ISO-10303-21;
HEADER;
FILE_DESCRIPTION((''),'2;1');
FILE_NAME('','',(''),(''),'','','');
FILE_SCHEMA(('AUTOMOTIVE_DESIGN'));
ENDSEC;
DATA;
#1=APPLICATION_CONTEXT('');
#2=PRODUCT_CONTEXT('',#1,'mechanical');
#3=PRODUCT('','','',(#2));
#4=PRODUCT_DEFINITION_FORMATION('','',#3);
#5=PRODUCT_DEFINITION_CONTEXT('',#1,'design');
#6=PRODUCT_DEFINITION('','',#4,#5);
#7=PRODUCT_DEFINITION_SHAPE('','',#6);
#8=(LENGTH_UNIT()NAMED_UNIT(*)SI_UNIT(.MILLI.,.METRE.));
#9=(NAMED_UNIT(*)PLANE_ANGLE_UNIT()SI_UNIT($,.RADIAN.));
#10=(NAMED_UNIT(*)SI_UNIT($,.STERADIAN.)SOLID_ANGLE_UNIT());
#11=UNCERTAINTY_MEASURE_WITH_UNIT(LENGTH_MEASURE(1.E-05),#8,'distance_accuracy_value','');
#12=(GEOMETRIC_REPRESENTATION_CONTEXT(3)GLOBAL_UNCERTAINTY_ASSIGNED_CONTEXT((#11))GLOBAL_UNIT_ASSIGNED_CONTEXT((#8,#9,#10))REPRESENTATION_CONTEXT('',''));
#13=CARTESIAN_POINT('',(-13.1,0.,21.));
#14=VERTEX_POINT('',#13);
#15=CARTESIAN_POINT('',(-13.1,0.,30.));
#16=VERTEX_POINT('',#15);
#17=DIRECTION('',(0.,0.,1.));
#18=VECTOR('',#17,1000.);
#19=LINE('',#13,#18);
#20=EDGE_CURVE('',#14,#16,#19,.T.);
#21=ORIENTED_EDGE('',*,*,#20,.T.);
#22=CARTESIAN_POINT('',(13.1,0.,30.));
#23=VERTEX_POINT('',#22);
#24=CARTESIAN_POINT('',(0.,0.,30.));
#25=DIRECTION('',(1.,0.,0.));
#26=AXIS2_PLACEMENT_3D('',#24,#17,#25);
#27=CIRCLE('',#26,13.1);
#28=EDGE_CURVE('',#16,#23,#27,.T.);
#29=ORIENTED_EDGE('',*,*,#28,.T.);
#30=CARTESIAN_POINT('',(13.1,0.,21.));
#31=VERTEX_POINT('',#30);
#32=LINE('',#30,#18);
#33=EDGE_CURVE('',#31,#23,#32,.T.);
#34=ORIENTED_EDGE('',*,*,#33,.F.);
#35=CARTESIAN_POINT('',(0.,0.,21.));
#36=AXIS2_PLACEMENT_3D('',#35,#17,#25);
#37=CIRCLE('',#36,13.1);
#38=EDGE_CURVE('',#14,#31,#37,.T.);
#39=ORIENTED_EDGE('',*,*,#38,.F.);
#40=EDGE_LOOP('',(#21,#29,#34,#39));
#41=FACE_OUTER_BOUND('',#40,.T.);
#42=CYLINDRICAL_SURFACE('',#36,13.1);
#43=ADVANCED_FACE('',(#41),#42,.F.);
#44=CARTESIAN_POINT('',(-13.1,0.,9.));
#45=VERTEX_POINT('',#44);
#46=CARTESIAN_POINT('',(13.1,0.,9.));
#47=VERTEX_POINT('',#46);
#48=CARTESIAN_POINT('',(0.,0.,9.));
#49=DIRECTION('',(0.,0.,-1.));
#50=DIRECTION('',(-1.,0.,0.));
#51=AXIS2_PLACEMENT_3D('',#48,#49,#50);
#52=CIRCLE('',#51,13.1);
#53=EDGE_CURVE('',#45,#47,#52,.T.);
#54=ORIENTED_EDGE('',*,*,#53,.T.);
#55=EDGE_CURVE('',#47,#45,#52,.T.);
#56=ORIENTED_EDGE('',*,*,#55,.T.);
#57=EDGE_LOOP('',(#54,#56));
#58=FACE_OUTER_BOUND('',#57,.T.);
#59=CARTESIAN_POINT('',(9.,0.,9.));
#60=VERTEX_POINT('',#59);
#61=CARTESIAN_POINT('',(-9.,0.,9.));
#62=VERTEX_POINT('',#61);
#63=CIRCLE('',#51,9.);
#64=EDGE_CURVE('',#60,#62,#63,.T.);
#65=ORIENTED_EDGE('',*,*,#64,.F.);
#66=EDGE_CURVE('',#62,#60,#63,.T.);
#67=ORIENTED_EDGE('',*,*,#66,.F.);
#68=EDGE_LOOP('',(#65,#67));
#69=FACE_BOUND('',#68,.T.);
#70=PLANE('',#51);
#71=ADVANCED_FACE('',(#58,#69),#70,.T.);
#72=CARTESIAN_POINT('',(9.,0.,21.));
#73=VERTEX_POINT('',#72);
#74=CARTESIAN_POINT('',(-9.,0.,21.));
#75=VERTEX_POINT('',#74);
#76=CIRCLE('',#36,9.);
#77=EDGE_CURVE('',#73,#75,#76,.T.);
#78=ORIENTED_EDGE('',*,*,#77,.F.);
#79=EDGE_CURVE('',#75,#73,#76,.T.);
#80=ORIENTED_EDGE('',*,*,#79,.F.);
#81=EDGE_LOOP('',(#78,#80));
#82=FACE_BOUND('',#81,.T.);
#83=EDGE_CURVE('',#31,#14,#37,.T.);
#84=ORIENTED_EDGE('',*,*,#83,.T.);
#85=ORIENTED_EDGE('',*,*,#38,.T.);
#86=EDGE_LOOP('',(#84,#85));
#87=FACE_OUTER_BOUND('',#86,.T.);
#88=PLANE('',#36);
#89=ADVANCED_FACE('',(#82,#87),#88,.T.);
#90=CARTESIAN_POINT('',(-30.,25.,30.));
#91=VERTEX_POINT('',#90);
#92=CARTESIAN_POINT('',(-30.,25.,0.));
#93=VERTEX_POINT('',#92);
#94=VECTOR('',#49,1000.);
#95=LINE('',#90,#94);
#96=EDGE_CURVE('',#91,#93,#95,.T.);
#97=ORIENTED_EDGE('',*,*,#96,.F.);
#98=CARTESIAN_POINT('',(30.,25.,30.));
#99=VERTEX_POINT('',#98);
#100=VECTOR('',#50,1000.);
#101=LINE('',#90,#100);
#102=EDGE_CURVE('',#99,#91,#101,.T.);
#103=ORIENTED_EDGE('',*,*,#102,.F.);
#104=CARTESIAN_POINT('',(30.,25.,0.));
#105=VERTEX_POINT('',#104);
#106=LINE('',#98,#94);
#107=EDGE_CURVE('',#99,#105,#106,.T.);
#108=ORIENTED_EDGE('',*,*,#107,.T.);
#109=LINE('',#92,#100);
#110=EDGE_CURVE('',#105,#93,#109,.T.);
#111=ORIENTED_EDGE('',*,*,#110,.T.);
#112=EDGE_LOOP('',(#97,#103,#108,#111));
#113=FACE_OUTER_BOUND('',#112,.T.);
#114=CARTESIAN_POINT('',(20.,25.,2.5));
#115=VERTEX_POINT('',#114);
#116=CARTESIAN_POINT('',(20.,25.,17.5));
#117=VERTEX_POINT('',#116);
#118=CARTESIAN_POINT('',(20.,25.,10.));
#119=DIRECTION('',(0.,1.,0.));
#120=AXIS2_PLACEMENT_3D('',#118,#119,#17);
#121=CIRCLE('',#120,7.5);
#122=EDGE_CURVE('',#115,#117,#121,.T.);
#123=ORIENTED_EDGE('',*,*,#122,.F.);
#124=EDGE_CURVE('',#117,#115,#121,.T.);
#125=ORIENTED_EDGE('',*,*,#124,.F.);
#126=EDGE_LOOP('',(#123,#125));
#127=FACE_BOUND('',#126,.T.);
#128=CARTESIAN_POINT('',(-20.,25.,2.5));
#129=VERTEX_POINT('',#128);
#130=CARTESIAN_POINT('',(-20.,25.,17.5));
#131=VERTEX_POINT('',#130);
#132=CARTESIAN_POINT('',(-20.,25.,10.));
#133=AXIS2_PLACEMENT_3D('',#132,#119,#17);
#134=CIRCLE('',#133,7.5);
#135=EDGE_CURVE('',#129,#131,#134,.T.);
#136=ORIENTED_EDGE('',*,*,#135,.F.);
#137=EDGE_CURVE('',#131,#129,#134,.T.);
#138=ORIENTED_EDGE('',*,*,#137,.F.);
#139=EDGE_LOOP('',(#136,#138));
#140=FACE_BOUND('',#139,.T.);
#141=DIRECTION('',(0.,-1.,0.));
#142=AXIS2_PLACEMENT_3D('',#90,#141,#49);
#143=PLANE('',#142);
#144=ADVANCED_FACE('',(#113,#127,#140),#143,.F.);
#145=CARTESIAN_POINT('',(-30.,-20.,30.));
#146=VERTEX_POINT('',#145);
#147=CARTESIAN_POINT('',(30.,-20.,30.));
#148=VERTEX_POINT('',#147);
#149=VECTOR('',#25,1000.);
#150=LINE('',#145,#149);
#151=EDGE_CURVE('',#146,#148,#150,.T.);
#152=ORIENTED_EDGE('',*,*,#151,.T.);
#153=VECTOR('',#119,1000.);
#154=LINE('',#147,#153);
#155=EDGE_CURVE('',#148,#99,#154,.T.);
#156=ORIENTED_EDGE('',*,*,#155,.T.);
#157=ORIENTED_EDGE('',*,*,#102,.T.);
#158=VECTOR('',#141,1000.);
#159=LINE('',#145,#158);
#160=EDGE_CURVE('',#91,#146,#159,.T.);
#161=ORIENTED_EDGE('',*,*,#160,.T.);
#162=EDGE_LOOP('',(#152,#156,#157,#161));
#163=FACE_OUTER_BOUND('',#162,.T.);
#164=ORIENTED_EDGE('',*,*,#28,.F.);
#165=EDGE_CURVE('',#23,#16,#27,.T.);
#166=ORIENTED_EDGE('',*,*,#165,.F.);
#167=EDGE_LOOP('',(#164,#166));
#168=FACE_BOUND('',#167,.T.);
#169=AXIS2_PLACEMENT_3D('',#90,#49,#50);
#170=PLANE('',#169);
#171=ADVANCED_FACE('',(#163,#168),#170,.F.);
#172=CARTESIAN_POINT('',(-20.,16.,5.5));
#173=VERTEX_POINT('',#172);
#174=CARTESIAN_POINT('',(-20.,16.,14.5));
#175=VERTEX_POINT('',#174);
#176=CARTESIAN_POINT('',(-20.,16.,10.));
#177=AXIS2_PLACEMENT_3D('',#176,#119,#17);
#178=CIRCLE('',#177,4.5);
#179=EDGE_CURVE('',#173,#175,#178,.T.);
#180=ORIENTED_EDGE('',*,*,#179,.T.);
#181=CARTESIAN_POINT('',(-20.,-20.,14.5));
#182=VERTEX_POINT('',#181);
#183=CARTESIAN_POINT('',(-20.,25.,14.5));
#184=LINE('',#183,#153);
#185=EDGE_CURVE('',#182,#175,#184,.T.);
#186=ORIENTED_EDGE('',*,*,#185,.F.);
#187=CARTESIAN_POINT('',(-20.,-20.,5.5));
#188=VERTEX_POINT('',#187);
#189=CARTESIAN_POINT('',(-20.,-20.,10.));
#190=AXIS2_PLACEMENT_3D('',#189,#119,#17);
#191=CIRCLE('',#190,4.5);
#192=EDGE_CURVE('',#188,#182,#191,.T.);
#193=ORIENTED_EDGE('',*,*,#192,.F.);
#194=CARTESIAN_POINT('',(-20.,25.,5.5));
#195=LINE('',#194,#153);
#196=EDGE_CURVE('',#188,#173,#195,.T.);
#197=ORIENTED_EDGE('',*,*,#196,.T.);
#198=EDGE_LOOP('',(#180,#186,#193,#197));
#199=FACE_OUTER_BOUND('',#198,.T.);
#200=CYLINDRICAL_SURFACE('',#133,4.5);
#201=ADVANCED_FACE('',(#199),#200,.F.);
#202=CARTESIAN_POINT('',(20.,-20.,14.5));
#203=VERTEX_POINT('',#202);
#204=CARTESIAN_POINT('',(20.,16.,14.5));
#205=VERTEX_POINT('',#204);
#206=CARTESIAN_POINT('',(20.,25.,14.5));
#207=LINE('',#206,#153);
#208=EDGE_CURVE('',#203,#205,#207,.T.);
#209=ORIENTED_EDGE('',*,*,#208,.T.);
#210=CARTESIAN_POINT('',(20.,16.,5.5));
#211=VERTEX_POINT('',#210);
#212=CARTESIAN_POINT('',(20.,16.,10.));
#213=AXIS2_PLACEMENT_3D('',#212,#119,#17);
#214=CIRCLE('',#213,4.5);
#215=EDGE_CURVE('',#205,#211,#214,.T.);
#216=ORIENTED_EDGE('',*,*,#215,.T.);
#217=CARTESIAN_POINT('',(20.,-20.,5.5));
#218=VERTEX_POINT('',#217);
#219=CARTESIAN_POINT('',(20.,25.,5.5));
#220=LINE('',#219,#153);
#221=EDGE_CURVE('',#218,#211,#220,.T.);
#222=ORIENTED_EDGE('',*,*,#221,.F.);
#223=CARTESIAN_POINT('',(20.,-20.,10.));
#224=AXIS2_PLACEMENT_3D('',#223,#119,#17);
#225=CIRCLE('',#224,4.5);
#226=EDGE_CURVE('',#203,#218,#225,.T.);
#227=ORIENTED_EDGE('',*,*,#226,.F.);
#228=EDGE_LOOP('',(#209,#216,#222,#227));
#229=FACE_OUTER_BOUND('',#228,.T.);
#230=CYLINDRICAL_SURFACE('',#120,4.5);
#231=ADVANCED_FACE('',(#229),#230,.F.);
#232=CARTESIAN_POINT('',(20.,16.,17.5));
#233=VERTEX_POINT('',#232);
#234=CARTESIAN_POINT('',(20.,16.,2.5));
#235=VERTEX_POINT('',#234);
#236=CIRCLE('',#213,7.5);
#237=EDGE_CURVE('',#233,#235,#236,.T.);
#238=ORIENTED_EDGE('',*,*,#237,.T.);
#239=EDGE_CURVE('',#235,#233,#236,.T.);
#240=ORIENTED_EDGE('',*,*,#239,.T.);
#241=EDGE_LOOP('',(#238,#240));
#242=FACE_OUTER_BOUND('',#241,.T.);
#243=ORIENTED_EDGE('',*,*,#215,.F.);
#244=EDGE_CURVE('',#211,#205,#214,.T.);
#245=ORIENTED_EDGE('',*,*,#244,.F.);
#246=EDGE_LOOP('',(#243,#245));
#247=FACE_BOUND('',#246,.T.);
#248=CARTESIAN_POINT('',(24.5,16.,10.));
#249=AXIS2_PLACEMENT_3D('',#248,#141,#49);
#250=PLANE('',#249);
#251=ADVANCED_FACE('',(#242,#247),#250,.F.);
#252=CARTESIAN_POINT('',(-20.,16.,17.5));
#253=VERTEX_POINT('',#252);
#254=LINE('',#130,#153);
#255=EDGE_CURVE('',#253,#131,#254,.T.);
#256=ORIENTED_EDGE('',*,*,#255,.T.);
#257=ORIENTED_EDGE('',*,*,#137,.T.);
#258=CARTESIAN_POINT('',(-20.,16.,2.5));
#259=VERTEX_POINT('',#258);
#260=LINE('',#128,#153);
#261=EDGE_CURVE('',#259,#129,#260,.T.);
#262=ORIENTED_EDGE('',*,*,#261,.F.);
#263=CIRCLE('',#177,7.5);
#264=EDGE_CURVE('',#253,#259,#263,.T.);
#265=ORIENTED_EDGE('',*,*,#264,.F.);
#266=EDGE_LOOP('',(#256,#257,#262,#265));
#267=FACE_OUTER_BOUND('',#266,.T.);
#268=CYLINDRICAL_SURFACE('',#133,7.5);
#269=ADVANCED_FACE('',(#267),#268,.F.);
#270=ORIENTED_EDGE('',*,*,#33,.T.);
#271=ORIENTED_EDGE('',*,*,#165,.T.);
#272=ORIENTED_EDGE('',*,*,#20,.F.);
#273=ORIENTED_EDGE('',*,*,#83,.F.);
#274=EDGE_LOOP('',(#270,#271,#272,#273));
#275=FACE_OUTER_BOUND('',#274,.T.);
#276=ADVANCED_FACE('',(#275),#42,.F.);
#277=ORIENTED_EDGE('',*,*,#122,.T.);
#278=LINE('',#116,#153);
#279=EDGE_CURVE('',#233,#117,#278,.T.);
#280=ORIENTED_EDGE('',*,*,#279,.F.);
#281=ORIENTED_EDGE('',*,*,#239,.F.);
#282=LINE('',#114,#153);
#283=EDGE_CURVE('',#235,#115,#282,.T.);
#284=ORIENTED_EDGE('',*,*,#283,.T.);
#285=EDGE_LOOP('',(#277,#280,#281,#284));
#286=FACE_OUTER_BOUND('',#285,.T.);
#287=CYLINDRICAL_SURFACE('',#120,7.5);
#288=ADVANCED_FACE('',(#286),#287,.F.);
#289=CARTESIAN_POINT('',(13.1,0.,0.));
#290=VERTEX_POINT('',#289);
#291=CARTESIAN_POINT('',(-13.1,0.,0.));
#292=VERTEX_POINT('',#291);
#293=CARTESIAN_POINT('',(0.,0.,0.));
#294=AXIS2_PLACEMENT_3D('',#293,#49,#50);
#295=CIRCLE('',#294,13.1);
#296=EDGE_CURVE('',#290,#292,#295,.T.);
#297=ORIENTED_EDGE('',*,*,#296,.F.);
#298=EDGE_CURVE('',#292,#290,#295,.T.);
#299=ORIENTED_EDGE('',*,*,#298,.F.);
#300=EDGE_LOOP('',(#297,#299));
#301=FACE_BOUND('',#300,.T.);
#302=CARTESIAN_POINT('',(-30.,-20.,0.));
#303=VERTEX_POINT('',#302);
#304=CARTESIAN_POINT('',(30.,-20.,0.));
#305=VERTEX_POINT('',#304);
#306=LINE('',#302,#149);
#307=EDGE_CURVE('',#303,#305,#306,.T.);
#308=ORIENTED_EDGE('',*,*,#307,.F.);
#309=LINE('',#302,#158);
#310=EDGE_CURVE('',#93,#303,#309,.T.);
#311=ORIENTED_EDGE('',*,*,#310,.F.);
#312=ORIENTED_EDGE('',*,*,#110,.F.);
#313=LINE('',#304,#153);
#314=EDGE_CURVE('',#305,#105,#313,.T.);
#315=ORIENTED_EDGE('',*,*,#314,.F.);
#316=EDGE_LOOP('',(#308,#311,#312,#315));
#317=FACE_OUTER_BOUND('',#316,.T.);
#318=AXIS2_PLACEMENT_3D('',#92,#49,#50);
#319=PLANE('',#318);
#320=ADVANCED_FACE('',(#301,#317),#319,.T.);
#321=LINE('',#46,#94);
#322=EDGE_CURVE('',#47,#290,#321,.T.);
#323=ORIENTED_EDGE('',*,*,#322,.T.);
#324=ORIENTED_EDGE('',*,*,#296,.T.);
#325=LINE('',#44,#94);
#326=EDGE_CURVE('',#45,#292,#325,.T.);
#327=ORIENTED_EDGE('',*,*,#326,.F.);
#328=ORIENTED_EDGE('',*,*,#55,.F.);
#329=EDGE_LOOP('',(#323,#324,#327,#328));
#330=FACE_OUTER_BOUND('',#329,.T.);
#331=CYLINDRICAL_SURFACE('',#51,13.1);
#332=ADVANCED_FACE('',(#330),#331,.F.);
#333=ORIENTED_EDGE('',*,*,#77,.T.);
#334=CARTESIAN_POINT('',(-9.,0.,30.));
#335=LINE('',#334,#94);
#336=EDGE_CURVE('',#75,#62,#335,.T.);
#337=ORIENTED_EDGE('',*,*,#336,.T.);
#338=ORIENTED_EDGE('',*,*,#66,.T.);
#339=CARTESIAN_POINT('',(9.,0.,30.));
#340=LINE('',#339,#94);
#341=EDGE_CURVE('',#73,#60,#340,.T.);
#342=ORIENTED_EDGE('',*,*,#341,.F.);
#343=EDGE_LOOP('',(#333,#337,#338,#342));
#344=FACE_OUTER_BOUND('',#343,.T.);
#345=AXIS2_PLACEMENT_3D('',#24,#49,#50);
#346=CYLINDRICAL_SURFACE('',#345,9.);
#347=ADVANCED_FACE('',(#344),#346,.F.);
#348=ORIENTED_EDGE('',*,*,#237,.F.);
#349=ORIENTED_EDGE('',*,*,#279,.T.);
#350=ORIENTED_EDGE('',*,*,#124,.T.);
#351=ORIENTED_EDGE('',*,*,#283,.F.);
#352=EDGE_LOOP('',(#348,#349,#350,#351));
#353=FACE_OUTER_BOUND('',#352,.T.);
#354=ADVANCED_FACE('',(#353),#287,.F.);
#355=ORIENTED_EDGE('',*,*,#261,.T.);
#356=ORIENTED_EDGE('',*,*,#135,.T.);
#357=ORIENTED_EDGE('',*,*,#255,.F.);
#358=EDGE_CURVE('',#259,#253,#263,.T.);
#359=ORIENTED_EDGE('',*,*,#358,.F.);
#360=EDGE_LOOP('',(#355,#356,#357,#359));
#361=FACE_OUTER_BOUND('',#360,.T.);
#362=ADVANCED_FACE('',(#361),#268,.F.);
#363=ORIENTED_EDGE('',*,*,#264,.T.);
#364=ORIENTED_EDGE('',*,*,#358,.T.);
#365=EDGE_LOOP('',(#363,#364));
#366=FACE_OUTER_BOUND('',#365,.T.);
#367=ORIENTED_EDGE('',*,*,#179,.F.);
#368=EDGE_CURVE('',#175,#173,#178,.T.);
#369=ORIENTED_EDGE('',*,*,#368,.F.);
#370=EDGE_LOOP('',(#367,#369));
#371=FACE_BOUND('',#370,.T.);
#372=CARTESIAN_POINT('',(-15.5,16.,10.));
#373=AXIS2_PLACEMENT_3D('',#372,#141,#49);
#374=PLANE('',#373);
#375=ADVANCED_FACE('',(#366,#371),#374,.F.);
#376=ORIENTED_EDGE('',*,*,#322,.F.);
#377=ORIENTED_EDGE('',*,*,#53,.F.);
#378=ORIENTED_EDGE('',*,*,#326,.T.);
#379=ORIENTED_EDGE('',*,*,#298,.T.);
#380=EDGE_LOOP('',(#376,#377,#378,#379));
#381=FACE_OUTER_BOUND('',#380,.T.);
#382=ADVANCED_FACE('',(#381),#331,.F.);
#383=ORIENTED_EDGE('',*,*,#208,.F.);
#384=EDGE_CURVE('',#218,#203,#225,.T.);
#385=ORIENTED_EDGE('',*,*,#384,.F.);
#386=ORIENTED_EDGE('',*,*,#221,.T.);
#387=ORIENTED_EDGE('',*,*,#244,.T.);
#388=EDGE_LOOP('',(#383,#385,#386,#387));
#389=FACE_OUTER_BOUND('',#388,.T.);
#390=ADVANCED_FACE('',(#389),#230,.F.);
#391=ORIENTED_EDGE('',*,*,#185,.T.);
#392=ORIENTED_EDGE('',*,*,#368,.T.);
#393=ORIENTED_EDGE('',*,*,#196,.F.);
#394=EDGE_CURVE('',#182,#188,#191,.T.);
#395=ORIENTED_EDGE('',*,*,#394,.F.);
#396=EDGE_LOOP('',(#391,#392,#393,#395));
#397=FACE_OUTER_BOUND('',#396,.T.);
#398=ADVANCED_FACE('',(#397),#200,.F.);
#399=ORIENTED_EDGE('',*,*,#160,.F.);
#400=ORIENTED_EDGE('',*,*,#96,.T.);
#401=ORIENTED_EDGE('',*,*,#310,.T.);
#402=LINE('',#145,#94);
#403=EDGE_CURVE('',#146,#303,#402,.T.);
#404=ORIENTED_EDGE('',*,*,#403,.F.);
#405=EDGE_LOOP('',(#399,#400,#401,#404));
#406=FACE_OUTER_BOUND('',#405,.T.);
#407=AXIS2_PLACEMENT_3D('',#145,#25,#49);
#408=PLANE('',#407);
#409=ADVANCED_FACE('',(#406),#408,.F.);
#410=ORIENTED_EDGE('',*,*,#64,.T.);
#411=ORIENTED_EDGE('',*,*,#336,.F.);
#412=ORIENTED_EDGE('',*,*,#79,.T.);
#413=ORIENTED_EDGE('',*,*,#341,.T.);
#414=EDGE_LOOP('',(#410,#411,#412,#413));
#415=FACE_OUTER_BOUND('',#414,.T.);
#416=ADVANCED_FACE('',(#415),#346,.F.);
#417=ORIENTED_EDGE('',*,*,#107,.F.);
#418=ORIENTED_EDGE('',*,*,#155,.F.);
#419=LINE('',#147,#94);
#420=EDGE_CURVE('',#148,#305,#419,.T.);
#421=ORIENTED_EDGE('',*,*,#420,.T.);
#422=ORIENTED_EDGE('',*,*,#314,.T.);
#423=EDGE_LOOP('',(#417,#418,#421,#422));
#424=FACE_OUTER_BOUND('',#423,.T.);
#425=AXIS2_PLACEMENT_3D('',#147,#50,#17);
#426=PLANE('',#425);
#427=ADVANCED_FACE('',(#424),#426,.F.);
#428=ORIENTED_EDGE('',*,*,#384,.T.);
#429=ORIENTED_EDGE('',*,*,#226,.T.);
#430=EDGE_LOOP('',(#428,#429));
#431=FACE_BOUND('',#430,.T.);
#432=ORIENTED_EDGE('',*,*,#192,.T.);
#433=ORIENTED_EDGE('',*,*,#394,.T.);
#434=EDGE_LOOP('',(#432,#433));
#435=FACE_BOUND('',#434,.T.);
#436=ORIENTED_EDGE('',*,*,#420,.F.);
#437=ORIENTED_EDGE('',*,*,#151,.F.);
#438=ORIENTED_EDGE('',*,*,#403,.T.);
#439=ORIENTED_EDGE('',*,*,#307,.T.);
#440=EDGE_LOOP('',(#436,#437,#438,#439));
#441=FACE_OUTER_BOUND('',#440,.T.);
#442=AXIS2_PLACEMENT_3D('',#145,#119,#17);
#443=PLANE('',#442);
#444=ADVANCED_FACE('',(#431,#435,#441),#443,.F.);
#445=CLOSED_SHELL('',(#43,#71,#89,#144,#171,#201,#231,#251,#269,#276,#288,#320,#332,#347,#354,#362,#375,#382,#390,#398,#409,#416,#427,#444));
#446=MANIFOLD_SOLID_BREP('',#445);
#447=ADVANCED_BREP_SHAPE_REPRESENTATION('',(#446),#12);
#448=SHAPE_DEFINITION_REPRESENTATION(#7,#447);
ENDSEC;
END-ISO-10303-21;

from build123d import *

# Parameters (mm, degrees)
SKETCH1_W                                            = 60
SKETCH1_H                                            = 45
SKETCH1_R                                            = 9
BOSS_EXTRUDE1_DEPTH                                  = 30
HOLE_SIZE_PER_SOCKET_HEAD_CAP_SCREW_TYPE_D           = 9
HOLE_SIZE_PER_SOCKET_HEAD_CAP_SCREW_TYPE_CBORE_D     = 15
HOLE_SIZE_PER_SOCKET_HEAD_CAP_SCREW_TYPE_CBORE_DEPTH = 9
SKETCH2_R                                            = 13.1
EXTRUDE1_DEPTH                                       = 9
EXTRUDE2_START                                       = -9
SKETCH3_R                                            = 13.1
EXTRUDE2_DEPTH                                       = 9


with BuildPart() as part:
    # Sketch1 → Boss-Extrude1 (new body)
    with BuildSketch(Plane.XY):
        with Locations((0, 2.5)):
            Rectangle(SKETCH1_W, SKETCH1_H)
        Circle(SKETCH1_R, mode=Mode.SUBTRACT)
    extrude(amount=BOSS_EXTRUDE1_DEPTH)

    # Hole size per socket head cap screw type1 (through all)
    with Locations(Plane(origin=(0, 25, 0), x_dir=(-1, 0, 0), z_dir=(0, 1, 0))):
        with Locations((20, 10), (-20, 10)):
            CounterBoreHole(HOLE_SIZE_PER_SOCKET_HEAD_CAP_SCREW_TYPE_D / 2, HOLE_SIZE_PER_SOCKET_HEAD_CAP_SCREW_TYPE_CBORE_D / 2, HOLE_SIZE_PER_SOCKET_HEAD_CAP_SCREW_TYPE_CBORE_DEPTH)

    # Sketch2 → Extrude1 (cut)
    with BuildSketch(Plane.XY.offset(30)):
        Circle(SKETCH2_R)
    extrude(amount=-EXTRUDE1_DEPTH, mode=Mode.SUBTRACT)

    # Sketch3 → Extrude2 (cut)
    with BuildSketch(Plane(origin=(0, 0, 0), x_dir=(-1, 0, 0), z_dir=(0, 0, -1)).offset(EXTRUDE2_START)):
        with Locations(Location((0, 0, 0), (0, 0, 180))):
            Circle(SKETCH3_R)
    extrude(amount=EXTRUDE2_DEPTH, mode=Mode.SUBTRACT)


solid = part.part
